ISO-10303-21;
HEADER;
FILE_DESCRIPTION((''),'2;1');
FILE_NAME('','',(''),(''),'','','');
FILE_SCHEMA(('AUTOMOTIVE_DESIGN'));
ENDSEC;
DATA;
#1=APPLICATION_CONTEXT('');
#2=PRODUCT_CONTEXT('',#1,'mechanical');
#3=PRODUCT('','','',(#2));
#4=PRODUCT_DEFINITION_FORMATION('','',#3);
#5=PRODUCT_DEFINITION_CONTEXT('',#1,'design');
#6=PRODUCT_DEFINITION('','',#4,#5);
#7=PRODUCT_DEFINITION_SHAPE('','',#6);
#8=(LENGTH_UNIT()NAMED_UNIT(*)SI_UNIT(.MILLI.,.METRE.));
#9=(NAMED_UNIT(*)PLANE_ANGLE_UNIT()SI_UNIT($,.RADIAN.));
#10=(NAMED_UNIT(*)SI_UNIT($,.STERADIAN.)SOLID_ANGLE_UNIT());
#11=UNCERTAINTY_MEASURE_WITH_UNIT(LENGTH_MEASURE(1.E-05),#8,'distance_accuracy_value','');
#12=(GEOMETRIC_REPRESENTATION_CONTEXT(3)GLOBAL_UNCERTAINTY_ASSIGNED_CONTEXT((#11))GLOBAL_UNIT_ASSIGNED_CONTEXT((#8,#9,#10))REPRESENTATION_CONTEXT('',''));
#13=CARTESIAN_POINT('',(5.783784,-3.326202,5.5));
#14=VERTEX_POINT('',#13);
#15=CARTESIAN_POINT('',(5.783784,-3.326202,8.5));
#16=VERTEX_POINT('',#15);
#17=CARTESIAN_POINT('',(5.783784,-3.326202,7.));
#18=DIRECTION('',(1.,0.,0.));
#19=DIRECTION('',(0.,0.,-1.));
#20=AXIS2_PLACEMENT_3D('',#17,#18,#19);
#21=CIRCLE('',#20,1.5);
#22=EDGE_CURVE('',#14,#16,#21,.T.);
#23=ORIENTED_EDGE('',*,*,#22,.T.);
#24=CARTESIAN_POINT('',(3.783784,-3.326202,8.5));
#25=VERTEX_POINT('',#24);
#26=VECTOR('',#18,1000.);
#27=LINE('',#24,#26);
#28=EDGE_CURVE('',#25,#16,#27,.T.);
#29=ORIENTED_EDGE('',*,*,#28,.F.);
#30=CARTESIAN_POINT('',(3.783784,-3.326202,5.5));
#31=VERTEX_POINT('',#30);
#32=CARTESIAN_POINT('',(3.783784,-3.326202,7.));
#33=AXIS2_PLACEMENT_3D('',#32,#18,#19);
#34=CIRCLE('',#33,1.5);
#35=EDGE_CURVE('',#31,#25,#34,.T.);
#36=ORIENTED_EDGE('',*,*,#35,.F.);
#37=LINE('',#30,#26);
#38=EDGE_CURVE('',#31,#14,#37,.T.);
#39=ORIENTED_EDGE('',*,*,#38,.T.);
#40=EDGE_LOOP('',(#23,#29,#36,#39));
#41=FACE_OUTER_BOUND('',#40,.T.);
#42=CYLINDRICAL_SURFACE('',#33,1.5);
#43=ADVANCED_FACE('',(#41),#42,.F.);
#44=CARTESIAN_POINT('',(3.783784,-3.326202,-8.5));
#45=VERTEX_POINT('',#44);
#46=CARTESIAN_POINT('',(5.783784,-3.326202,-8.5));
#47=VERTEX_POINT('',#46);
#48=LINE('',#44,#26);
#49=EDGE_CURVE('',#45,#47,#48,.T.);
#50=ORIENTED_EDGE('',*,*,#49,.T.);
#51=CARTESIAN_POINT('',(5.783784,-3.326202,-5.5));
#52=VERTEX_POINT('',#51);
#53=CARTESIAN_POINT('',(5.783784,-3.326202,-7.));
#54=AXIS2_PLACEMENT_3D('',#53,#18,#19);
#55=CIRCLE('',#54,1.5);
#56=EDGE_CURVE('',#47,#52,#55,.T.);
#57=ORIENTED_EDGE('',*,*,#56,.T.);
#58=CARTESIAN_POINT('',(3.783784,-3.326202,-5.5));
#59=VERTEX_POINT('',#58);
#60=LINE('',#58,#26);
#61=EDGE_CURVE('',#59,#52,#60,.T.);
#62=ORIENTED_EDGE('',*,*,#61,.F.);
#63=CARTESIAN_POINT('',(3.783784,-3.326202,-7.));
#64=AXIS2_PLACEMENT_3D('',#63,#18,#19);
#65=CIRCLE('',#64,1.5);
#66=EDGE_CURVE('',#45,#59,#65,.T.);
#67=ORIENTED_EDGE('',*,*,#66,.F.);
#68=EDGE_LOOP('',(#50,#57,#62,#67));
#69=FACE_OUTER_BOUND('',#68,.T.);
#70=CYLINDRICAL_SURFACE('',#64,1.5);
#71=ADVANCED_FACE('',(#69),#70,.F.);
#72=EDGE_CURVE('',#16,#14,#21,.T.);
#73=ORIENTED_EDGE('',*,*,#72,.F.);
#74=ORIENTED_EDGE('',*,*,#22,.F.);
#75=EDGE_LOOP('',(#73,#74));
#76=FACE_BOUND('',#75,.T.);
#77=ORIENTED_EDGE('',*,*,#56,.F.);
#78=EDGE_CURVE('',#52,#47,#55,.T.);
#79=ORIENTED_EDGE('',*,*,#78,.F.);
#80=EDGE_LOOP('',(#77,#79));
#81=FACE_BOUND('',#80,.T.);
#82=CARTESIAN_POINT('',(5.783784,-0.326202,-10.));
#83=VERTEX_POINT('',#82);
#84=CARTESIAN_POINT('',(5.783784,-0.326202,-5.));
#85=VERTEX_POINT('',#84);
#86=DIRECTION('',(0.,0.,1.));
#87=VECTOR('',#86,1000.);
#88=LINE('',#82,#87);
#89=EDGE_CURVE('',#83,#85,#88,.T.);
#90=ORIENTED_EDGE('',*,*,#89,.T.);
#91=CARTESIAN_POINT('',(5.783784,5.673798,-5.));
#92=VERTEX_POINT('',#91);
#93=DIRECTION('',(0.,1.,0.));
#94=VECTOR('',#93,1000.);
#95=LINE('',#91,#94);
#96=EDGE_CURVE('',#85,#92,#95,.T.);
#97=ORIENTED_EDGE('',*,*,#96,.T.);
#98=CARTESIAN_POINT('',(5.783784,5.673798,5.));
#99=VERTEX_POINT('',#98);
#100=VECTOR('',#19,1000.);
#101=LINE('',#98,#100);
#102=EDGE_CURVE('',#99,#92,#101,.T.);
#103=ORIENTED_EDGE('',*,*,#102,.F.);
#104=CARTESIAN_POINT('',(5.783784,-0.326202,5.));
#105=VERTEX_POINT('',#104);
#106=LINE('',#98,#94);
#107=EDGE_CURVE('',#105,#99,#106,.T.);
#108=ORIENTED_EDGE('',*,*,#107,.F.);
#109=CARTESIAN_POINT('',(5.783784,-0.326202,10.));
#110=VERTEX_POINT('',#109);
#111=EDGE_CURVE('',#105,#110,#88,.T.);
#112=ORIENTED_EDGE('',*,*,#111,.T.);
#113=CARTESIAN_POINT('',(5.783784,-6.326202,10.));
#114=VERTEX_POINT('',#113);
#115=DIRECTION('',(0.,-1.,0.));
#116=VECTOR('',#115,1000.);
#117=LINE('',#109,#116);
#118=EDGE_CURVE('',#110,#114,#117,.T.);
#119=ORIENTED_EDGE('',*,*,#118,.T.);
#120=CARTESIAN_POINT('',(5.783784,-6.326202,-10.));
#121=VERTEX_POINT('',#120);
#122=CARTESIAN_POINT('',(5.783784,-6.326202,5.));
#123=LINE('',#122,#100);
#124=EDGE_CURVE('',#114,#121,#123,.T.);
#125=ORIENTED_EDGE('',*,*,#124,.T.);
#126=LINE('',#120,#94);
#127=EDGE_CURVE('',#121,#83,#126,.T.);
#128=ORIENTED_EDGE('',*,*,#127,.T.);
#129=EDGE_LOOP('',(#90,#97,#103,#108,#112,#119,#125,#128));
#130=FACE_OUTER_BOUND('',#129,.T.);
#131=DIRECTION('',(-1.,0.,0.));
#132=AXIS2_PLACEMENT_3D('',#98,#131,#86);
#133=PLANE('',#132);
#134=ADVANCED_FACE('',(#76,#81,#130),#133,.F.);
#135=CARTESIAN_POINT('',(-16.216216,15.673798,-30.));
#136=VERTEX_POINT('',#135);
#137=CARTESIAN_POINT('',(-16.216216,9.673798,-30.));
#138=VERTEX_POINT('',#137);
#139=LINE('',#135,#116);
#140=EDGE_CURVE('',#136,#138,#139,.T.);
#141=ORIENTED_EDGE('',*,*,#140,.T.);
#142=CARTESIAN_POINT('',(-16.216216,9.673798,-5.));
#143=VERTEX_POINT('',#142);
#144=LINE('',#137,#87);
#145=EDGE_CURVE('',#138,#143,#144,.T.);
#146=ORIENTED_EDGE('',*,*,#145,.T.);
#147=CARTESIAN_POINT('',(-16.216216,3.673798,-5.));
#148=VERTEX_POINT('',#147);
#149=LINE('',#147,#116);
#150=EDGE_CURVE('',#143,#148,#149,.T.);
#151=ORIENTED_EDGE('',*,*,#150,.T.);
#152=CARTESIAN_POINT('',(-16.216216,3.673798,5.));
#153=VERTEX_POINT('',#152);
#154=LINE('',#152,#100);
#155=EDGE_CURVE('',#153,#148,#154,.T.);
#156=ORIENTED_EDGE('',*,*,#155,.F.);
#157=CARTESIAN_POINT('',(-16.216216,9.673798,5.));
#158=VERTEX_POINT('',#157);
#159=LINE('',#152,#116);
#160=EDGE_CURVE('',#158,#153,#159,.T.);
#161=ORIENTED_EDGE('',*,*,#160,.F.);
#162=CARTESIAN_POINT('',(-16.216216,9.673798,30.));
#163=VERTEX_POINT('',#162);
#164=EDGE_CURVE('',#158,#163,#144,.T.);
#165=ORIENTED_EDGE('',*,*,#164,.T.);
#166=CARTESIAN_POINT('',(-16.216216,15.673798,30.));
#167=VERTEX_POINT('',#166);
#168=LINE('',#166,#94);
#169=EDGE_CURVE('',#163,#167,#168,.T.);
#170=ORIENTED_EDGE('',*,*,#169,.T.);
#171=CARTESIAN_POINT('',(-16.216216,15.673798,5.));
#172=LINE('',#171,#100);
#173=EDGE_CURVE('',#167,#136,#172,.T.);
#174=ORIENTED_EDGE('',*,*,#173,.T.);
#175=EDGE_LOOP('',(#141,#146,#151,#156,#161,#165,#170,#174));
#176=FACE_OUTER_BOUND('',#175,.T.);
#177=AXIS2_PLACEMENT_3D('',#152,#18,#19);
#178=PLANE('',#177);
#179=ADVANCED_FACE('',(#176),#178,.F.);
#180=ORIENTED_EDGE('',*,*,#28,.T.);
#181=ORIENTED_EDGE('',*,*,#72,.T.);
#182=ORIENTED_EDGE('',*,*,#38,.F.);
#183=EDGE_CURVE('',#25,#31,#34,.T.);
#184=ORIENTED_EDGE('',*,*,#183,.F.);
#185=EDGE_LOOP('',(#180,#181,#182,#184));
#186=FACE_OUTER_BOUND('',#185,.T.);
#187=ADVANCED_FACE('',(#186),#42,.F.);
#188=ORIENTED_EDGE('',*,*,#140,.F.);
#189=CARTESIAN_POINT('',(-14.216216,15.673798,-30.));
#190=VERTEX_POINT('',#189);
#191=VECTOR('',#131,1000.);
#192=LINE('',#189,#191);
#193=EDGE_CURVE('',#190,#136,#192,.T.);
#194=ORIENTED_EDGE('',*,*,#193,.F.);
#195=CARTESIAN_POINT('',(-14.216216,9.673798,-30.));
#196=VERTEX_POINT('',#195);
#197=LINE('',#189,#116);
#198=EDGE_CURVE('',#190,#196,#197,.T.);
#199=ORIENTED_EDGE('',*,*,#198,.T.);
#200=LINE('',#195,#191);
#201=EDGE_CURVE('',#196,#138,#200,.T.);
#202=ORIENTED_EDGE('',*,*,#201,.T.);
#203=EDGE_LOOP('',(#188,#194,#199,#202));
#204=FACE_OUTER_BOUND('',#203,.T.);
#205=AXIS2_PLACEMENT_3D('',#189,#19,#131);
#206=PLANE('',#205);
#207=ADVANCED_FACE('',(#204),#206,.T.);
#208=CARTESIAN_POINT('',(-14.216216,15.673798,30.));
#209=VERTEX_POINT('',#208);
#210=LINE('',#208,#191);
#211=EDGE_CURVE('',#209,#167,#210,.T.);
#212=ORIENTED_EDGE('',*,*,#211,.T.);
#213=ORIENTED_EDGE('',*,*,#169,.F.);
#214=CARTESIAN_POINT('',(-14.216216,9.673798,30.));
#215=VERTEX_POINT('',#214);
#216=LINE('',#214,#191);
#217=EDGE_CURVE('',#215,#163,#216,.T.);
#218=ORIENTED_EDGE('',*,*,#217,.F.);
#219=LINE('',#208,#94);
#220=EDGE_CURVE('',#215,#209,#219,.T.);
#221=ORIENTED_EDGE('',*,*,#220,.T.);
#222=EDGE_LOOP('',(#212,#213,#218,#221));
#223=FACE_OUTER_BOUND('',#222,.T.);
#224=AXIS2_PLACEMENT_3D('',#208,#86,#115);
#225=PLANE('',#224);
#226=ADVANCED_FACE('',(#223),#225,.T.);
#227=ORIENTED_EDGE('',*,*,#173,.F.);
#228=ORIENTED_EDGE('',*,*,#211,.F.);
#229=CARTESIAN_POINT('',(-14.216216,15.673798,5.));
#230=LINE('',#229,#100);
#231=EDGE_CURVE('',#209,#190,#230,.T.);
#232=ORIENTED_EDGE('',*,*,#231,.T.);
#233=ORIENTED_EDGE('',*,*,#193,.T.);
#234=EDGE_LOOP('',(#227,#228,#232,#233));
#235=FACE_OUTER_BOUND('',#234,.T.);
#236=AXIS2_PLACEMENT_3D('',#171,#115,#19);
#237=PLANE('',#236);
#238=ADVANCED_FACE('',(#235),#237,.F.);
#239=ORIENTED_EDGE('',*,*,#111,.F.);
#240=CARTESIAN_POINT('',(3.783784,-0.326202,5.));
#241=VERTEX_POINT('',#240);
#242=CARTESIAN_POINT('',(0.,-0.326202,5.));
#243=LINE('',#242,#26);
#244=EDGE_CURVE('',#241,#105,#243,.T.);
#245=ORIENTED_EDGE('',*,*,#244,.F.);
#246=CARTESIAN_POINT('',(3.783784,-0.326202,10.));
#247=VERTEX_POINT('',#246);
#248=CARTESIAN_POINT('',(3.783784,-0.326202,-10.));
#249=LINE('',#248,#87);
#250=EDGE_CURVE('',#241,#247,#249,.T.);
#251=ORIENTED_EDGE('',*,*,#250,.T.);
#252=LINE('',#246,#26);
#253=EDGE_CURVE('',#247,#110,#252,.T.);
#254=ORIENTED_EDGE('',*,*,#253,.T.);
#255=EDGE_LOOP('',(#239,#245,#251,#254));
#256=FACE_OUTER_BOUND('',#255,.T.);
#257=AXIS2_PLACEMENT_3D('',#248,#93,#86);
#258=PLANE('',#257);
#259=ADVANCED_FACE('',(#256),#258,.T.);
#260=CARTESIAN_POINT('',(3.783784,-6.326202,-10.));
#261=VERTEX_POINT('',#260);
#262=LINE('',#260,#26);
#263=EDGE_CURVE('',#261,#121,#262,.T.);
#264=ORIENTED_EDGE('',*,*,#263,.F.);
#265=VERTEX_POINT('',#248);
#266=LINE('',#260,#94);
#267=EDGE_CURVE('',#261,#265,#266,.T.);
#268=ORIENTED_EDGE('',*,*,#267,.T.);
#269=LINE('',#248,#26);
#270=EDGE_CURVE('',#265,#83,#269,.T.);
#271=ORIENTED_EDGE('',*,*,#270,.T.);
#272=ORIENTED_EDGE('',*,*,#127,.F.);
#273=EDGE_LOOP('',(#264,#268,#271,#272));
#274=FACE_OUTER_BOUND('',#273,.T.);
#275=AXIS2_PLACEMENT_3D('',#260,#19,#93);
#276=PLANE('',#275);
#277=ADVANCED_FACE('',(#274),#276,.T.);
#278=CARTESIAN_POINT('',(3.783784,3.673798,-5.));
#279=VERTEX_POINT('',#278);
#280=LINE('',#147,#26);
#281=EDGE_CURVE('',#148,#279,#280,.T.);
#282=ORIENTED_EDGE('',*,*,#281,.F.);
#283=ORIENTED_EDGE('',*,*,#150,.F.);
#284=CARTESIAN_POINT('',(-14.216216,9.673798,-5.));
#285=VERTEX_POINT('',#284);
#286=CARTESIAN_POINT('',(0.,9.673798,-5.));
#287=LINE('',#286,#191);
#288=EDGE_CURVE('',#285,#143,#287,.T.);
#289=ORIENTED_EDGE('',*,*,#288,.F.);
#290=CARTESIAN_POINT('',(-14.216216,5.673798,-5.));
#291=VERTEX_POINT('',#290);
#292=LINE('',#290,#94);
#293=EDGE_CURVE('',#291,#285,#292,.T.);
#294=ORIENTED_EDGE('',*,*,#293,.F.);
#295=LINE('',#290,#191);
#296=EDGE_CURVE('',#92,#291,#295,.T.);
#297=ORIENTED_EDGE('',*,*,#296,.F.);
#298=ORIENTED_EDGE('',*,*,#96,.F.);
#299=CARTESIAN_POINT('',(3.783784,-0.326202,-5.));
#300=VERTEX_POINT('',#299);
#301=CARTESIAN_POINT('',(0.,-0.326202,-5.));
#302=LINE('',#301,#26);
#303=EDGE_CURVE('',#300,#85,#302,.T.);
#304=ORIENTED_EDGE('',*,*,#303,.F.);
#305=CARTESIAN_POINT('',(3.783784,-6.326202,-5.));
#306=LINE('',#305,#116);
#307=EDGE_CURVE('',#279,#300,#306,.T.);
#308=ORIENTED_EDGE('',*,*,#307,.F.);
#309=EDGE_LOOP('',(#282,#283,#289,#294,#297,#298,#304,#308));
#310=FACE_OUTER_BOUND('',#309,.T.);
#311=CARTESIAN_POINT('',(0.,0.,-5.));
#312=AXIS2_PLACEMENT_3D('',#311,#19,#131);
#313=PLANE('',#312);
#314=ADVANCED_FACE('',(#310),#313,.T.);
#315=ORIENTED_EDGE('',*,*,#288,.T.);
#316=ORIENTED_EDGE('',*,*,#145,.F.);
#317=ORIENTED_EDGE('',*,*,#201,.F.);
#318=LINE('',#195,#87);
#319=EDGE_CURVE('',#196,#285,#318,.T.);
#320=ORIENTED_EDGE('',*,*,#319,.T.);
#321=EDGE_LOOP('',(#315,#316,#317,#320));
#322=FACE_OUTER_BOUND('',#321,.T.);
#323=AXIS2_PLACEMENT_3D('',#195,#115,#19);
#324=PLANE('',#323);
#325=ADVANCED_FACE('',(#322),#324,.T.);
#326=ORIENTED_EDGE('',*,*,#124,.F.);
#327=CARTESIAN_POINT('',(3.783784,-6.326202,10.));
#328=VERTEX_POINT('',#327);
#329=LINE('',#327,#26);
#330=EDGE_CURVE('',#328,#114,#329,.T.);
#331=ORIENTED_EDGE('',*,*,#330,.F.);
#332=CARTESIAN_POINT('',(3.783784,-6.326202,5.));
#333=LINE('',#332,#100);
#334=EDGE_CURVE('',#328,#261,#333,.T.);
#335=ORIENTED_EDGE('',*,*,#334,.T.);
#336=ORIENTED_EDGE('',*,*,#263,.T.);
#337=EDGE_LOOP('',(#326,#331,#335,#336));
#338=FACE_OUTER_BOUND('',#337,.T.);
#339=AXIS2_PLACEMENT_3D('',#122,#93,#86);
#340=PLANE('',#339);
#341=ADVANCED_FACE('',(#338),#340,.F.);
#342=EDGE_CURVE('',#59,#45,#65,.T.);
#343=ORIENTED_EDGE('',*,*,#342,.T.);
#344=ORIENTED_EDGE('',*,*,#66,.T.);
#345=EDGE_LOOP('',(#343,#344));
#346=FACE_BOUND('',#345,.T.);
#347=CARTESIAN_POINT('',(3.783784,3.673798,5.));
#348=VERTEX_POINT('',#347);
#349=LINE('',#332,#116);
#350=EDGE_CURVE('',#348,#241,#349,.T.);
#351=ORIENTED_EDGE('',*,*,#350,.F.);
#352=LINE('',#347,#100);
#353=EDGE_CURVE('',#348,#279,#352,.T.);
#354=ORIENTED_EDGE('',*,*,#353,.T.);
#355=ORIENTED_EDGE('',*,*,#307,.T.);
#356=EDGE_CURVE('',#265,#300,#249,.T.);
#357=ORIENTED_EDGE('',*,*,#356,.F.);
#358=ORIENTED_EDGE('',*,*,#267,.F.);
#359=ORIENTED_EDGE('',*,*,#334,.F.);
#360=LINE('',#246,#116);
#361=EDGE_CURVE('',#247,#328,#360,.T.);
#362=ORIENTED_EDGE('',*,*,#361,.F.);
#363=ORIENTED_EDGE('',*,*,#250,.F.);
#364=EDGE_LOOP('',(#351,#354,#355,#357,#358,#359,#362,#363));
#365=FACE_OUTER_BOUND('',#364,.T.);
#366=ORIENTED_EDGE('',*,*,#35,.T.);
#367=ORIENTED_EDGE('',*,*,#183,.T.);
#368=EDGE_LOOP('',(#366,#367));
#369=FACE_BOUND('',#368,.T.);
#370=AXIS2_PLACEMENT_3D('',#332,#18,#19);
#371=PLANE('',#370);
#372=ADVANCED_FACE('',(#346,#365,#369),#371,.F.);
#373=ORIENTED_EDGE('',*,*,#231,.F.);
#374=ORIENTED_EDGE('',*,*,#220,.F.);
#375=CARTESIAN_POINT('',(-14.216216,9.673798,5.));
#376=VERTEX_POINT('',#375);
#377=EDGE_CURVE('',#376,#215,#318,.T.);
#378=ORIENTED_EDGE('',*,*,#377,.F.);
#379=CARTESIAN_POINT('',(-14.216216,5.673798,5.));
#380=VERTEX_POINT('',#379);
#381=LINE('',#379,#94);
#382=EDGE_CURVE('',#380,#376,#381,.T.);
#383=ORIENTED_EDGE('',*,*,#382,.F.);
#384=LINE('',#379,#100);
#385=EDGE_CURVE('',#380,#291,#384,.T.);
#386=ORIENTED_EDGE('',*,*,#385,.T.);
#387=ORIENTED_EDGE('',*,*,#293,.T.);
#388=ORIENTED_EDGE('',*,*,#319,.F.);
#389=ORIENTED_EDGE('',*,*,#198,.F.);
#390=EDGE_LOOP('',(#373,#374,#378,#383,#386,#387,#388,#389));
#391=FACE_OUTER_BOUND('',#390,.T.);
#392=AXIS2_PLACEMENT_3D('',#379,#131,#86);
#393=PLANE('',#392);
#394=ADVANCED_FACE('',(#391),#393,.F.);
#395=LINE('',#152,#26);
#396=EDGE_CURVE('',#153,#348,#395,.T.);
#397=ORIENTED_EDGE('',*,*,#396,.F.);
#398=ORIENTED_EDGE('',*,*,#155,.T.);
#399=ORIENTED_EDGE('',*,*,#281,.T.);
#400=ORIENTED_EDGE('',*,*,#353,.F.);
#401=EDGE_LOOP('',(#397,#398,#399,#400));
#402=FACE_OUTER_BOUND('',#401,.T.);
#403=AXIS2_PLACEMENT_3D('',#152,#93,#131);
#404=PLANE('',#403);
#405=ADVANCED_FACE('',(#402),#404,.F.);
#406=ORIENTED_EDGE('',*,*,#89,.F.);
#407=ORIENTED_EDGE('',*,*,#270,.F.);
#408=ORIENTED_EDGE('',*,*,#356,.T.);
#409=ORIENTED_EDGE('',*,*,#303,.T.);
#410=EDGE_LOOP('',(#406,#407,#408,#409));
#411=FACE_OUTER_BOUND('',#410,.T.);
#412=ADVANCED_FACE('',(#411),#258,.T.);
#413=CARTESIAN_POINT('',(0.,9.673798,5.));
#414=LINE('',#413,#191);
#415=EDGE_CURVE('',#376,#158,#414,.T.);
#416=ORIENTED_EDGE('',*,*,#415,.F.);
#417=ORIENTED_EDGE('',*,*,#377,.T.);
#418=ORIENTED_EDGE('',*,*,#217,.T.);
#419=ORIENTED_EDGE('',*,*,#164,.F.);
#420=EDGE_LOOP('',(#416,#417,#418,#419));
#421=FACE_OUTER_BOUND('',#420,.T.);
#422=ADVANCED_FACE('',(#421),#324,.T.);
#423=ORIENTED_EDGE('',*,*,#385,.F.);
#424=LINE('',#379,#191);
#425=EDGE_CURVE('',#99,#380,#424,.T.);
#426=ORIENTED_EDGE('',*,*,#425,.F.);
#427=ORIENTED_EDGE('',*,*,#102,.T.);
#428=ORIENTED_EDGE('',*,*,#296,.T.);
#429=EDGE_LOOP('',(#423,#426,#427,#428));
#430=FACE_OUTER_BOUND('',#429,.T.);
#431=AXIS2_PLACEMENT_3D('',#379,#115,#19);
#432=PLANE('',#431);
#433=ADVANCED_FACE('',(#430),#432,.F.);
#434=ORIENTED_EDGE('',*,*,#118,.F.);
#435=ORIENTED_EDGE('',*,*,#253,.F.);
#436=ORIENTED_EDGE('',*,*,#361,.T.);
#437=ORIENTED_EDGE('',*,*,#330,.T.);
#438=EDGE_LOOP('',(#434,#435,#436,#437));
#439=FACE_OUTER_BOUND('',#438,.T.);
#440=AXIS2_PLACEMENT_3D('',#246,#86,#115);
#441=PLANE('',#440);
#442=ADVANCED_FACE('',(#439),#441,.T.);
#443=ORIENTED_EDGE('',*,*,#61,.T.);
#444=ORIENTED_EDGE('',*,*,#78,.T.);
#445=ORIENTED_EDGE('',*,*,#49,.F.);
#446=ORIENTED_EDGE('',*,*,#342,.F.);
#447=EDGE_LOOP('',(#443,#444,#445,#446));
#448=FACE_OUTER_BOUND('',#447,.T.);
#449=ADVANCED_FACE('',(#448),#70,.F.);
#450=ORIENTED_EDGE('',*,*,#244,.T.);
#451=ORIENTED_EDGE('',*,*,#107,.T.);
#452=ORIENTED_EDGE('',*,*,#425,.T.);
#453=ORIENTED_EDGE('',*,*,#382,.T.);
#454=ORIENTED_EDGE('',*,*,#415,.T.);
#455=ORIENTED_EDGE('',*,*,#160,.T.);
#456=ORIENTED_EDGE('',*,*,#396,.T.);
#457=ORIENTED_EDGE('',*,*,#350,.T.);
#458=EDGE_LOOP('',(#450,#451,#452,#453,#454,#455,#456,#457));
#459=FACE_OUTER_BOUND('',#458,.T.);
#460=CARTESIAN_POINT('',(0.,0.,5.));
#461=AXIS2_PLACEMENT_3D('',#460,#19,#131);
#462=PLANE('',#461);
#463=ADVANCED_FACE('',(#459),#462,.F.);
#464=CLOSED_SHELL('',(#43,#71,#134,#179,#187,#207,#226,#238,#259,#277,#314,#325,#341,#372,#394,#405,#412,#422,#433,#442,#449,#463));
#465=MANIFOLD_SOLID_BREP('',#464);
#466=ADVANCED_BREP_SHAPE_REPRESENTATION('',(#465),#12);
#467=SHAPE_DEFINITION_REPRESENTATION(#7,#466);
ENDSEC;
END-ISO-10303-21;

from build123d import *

# Parameters (mm, degrees)
BOSS_EXTRUDE1_DEPTH = 5
SKETCH2_W           = 20
SKETCH2_H           = 6
SKETCH2_R           = 1.5
BOSS_EXTRUDE2_DEPTH = 2
SKETCH3_W           = 60
SKETCH3_H           = 6
BOSS_EXTRUDE3_DEPTH = 2


with BuildPart() as part:
    # Sketch1 → Boss-Extrude1 (new, symmetric)
    with BuildSketch(Plane.XY):
        Polygon((-14.216216216, 5.673798061), (-14.216216216, 15.673798061), (-16.216216216, 15.673798061), (-16.216216216, 3.673798061), (3.783783784, 3.673798061), (3.783783784, -6.326201939), (5.783783784, -6.326201939), (5.783783784, 5.673798061), align=None)
    extrude(amount=BOSS_EXTRUDE1_DEPTH, both=True)

    # Sketch2 → Boss-Extrude2 (add)
    with BuildSketch(Plane(origin=(5.783783784, 0, 0), x_dir=(0, 0, -1), z_dir=(1, 0, 0))):
        with Locations((0, -3.326201939)):
            Rectangle(SKETCH2_W, SKETCH2_H)
        with Locations((-7, -3.326201939)):
            Circle(SKETCH2_R, mode=Mode.SUBTRACT)
        with Locations((7, -3.326201939)):
            Circle(SKETCH2_R, mode=Mode.SUBTRACT)
    extrude(amount=-BOSS_EXTRUDE2_DEPTH)

    # Sketch3 → Boss-Extrude3 (add)
    with BuildSketch(Plane.ZY.offset(16.216216216)):
        with Locations((0, 12.673798061)):
            Rectangle(SKETCH3_W, SKETCH3_H)
    extrude(amount=-BOSS_EXTRUDE3_DEPTH)


solid = part.part
